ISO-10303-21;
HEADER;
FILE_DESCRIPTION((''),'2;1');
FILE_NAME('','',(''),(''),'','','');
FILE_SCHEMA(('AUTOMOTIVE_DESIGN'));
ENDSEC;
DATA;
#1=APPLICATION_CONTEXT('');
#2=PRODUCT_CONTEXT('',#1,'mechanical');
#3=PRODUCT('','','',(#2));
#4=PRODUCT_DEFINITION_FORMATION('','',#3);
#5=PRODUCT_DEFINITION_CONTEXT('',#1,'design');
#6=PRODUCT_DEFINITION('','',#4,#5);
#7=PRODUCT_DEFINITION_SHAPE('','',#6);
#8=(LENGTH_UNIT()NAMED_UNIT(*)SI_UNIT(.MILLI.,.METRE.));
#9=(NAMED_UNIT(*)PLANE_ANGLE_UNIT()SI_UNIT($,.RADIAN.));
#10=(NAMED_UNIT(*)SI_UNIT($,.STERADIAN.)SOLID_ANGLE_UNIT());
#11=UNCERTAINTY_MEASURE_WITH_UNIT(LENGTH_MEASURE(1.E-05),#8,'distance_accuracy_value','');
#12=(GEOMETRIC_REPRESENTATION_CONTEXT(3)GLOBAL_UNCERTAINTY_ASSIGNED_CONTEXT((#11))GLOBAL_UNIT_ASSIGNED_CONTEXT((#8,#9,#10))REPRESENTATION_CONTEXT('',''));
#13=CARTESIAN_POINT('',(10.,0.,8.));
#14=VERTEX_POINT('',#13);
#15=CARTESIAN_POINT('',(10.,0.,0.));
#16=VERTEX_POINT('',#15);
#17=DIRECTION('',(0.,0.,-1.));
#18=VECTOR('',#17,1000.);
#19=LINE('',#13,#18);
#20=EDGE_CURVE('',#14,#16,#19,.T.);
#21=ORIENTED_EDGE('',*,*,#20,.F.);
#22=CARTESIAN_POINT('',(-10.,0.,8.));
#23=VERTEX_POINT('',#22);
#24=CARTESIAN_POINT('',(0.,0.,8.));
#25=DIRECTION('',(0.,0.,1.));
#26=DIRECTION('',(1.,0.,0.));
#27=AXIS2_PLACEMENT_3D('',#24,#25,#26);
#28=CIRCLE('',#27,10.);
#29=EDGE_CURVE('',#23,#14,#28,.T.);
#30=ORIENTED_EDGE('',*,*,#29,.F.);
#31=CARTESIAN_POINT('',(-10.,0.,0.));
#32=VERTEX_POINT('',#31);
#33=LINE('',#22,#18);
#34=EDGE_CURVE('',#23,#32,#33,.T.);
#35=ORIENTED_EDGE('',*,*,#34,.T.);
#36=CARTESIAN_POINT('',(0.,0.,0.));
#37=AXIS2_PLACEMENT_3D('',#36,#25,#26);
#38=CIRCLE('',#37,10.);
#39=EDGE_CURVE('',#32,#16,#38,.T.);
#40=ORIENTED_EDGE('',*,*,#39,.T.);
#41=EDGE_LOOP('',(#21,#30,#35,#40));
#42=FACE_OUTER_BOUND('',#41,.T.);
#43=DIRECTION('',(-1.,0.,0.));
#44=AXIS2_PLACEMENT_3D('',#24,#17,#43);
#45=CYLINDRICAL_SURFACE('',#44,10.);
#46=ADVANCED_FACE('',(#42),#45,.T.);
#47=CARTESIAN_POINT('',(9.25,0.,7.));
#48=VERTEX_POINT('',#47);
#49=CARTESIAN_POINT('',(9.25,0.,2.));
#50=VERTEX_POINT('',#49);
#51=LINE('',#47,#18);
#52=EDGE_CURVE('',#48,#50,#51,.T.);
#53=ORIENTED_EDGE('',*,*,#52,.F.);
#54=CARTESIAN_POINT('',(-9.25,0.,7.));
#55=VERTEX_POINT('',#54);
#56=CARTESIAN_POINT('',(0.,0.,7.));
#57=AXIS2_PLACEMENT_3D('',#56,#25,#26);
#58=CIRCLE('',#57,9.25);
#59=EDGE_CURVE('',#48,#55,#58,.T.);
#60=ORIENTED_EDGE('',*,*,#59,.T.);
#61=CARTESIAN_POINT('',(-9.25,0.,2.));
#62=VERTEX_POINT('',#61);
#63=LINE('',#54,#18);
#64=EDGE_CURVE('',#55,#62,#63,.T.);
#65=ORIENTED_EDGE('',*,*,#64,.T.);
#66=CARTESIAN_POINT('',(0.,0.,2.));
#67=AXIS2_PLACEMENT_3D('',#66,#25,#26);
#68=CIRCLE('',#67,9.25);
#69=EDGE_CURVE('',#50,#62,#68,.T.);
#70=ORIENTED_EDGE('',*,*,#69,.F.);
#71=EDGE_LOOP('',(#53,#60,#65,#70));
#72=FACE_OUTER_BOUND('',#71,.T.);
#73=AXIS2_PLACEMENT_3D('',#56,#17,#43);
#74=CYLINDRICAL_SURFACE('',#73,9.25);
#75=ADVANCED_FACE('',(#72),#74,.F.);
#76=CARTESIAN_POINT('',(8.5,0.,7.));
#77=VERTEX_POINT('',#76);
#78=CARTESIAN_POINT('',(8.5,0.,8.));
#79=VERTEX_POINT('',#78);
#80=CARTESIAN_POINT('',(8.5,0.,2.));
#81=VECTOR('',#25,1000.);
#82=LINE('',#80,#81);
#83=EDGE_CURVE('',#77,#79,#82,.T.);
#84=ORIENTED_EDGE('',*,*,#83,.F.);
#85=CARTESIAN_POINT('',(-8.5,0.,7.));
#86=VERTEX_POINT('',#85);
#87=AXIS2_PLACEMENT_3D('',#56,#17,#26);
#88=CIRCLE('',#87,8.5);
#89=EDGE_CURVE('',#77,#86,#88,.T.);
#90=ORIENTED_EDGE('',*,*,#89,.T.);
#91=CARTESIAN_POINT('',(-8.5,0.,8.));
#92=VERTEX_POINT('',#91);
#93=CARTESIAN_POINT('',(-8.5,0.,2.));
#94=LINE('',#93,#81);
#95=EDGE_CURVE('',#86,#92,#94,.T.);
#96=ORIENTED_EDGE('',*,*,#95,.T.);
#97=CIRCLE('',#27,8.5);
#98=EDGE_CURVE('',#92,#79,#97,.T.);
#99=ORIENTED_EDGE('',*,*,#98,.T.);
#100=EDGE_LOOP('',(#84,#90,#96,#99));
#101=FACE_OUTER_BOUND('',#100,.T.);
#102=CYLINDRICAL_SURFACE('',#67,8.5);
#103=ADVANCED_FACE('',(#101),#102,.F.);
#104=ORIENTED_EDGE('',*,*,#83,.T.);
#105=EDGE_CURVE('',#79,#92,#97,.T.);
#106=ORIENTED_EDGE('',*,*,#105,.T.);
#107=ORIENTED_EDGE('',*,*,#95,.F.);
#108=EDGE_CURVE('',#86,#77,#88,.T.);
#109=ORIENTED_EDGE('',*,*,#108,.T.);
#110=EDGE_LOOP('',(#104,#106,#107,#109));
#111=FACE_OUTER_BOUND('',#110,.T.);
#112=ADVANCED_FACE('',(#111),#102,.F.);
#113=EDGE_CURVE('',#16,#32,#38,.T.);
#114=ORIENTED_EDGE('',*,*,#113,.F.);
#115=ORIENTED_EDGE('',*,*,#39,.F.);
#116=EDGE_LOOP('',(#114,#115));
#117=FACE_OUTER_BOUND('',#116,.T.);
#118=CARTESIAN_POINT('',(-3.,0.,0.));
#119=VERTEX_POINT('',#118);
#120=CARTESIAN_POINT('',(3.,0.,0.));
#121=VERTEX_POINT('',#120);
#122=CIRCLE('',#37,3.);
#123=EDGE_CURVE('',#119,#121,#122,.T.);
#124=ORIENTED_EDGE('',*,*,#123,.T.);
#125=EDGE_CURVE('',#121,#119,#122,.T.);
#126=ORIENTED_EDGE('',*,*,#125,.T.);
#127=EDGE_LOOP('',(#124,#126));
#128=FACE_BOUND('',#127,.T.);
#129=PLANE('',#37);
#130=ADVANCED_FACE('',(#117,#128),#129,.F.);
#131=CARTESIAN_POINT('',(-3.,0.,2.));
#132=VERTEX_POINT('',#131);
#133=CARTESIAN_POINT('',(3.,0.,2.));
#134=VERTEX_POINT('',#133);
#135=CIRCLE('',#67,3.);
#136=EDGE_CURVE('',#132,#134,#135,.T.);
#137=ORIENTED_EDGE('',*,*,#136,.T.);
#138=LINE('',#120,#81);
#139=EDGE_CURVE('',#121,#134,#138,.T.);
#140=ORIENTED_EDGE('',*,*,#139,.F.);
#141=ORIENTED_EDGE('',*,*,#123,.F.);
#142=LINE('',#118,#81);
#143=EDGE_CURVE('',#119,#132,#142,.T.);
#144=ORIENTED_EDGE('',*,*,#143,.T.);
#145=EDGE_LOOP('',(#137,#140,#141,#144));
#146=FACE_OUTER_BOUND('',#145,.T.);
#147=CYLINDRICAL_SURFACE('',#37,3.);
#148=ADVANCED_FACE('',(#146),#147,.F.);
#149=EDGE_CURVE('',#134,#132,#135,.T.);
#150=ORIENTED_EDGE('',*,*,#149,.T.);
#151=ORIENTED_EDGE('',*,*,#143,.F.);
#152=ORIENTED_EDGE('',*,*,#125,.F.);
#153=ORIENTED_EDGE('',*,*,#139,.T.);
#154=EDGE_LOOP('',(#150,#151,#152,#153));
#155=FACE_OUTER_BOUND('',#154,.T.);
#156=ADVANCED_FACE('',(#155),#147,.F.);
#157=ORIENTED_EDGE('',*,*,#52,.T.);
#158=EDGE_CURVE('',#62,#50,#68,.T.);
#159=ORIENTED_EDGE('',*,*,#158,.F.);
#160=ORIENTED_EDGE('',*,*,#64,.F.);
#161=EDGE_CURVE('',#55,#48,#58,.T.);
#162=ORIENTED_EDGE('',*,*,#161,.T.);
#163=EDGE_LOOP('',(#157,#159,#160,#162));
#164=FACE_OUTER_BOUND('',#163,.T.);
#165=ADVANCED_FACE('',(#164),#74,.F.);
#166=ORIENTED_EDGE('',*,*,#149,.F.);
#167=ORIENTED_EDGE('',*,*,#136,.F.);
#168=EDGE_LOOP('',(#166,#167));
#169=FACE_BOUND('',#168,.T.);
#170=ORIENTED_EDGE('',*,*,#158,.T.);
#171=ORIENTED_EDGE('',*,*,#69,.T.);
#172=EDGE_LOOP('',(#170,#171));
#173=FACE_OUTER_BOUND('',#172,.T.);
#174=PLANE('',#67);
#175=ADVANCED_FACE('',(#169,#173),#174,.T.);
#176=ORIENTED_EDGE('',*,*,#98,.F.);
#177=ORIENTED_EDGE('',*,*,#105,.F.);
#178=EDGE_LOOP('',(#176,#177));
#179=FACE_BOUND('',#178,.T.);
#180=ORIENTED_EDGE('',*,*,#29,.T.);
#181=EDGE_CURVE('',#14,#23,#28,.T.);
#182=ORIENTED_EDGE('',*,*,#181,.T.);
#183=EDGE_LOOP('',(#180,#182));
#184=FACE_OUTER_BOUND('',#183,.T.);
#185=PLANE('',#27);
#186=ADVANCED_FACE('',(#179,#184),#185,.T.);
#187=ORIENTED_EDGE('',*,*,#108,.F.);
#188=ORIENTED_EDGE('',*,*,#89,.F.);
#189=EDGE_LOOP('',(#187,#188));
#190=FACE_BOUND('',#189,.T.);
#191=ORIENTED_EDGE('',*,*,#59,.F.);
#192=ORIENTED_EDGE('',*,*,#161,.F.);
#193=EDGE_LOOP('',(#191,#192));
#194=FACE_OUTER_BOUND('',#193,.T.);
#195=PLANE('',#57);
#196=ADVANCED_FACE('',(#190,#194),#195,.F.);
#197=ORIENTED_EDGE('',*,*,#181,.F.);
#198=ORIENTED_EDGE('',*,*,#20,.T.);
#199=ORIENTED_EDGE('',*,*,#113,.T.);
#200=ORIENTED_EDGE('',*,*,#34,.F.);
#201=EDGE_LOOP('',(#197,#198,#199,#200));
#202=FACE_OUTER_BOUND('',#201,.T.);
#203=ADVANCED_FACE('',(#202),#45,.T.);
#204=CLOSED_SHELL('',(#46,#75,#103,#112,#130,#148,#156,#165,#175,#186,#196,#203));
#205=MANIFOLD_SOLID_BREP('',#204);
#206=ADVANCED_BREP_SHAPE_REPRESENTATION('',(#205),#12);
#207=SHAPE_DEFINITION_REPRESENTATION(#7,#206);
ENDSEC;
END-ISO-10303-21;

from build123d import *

# Parameters (mm, degrees)
SKETCH1_R           = 10
BOSS_EXTRUDE1_DEPTH = 8
SKETCH2_R           = 8.5
CUT_EXTRUDE1_DEPTH  = 6
SKETCH3_R           = 3
CUT_EXTRUDE2_DEPTH  = 16.362291496
SKETCH4_R           = 9.25
CUT_EXTRUDE3_DEPTH  = 5


with BuildPart() as part:
    # Sketch1 → Boss-Extrude1 (new body)
    with BuildSketch(Plane.XY):
        Circle(SKETCH1_R)
    extrude(amount=BOSS_EXTRUDE1_DEPTH)

    # Sketch2 → Cut-Extrude1 (cut)
    with BuildSketch(Plane.XY.offset(8)):
        Circle(SKETCH2_R)
    extrude(amount=-CUT_EXTRUDE1_DEPTH, mode=Mode.SUBTRACT)

    # Sketch3 → Cut-Extrude2 (cut, through all)
    with BuildSketch(Plane.XY.offset(2)):
        Circle(SKETCH3_R)
    extrude(amount=-CUT_EXTRUDE2_DEPTH, mode=Mode.SUBTRACT)

    # Sketch4 → Cut-Extrude3 (cut)
    with BuildSketch(Plane.XY.offset(2)):
        Circle(SKETCH4_R)
    extrude(amount=CUT_EXTRUDE3_DEPTH, mode=Mode.SUBTRACT)


solid = part.part
